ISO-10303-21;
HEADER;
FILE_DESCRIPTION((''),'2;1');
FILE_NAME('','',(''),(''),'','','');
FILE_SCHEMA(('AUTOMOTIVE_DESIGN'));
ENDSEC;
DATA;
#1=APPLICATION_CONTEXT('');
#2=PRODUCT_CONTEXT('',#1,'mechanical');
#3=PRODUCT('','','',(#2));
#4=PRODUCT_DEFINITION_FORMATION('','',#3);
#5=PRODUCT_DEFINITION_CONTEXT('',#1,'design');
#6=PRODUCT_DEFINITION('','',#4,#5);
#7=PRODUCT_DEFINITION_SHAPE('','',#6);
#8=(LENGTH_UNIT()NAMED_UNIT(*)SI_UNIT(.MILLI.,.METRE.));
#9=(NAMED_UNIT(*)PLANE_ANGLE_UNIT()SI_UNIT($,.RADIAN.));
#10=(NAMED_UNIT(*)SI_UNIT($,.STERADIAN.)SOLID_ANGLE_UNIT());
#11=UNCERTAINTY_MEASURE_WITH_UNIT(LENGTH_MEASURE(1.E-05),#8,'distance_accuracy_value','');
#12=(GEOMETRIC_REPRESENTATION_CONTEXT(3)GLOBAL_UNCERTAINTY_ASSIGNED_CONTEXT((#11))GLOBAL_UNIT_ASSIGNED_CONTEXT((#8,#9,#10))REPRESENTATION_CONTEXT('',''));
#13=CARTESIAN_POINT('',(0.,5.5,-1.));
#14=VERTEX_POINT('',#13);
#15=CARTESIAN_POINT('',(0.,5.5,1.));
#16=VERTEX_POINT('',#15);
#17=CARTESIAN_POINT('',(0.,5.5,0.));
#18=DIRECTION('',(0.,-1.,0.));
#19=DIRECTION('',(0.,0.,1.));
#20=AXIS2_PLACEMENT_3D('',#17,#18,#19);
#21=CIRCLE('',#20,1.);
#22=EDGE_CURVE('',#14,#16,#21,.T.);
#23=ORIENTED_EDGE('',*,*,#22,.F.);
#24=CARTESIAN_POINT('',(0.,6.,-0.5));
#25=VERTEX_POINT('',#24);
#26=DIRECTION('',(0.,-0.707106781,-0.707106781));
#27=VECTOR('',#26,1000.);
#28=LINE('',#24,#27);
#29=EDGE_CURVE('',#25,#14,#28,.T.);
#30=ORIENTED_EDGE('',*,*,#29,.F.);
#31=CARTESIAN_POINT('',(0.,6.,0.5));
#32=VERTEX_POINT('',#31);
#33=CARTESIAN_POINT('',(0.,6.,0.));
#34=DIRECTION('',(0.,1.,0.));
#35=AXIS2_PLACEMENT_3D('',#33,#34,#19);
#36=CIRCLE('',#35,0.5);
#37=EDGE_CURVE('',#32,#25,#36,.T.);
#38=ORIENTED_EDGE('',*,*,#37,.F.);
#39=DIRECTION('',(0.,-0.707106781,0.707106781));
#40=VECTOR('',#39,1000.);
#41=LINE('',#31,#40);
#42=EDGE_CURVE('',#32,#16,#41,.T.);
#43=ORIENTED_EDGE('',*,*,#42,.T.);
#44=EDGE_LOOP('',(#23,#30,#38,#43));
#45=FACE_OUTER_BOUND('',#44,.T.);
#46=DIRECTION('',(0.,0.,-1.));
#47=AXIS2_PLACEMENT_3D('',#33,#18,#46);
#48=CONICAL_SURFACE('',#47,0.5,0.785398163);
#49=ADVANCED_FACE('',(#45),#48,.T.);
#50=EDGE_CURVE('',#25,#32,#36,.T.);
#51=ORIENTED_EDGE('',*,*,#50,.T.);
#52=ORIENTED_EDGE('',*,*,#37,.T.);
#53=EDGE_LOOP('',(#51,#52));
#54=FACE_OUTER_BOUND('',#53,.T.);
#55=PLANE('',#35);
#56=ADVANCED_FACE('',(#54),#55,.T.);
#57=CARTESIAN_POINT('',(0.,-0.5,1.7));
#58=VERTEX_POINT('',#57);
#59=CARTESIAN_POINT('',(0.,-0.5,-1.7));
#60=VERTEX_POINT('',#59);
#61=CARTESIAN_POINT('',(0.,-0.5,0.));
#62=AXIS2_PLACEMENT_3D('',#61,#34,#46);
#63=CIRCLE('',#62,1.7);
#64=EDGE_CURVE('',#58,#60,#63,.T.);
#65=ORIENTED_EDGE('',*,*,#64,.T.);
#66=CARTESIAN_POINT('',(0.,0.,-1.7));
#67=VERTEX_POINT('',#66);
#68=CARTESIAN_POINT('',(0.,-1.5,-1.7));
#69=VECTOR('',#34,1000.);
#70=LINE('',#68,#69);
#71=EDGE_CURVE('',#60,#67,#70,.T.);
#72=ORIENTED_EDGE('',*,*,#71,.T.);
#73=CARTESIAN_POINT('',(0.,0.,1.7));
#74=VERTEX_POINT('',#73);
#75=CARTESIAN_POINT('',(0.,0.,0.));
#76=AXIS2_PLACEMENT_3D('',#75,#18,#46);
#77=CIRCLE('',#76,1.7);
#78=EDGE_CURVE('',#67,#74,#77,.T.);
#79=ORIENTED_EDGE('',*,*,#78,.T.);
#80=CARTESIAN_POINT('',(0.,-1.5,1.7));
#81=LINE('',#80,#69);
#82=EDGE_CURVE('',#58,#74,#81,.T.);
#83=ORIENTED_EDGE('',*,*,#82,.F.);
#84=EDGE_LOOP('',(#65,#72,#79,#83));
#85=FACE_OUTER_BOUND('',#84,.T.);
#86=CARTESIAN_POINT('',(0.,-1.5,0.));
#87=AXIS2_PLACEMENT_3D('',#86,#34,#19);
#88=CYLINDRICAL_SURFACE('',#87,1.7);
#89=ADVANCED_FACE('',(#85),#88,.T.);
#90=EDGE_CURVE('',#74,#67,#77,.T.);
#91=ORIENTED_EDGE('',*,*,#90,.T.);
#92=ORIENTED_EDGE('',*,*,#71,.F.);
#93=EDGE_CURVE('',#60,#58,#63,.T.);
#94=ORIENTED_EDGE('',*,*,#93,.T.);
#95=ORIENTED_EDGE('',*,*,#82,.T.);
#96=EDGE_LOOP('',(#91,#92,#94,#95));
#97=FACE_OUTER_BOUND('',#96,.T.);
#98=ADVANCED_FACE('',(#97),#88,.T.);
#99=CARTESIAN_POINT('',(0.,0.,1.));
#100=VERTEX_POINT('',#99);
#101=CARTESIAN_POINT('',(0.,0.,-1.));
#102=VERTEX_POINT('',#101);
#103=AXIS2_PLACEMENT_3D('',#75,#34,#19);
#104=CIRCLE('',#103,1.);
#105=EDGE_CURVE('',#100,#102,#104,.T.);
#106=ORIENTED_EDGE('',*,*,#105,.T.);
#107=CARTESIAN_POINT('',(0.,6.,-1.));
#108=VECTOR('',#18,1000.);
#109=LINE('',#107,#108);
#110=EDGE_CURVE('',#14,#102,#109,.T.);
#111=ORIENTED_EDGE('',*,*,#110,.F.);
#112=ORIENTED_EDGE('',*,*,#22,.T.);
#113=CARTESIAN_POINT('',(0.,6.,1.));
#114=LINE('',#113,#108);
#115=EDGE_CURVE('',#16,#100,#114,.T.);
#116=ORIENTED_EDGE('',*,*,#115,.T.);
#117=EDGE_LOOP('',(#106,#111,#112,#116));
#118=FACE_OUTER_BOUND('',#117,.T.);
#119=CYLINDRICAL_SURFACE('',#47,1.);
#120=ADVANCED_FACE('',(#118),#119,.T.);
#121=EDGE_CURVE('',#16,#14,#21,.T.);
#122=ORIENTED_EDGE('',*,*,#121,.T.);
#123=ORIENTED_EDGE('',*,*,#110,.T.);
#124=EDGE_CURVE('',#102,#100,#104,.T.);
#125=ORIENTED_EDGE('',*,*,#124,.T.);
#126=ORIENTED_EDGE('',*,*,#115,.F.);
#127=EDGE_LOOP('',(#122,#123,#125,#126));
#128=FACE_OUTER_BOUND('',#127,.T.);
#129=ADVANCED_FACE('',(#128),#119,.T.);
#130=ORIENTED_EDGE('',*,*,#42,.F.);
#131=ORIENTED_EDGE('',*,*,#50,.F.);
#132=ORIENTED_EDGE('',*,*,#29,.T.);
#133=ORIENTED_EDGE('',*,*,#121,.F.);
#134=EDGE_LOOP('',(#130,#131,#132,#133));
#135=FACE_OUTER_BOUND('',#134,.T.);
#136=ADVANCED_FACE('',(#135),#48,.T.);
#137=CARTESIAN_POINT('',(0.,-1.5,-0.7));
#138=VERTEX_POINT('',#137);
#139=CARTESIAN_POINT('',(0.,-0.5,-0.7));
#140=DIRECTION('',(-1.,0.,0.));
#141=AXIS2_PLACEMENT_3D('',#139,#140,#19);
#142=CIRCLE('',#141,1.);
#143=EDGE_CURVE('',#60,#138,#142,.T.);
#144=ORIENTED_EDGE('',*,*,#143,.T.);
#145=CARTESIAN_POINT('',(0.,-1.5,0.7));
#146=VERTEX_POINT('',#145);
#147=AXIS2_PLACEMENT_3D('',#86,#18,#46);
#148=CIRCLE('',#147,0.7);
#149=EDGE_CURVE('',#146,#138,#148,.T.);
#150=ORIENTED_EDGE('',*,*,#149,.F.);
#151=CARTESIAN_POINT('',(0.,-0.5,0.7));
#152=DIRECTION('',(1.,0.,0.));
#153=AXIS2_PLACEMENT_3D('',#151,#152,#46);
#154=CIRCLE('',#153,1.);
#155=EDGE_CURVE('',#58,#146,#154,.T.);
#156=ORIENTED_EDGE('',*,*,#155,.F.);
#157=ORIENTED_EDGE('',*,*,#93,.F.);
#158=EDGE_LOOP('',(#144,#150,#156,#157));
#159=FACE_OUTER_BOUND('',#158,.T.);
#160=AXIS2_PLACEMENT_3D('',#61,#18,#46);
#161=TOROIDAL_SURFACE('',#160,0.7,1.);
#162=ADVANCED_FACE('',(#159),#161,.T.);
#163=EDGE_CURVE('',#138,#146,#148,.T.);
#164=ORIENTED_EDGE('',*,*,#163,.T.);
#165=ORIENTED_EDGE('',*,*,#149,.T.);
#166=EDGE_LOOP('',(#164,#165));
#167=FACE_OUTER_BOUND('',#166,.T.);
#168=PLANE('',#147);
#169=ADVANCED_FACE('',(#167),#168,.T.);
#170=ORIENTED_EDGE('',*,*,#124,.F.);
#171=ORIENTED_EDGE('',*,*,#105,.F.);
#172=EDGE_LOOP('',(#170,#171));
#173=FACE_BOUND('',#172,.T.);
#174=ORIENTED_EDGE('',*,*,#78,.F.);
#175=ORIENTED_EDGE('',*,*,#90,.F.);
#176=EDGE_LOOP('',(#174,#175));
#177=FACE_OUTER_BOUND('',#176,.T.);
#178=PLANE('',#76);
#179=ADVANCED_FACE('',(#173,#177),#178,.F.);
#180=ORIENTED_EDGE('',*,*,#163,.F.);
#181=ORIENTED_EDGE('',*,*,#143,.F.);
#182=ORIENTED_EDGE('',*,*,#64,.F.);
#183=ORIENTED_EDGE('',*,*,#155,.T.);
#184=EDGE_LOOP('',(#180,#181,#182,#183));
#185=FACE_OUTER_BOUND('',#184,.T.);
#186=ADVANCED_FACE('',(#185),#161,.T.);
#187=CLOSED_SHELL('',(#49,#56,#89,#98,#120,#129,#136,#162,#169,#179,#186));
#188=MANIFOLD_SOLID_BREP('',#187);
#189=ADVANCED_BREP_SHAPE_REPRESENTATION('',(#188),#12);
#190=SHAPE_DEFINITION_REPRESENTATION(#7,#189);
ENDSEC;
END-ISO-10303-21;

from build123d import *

# Parameters (mm, degrees)
SKETCH1_R           = 1
BOSS_EXTRUDE1_DEPTH = 6
CHAMFER1_SIZE       = 0.5
SKETCH2_R           = 1.7
BOSS_EXTRUDE2_DEPTH = 1.5
FILLET1_R           = 1


with BuildPart() as part:
    # Sketch1 → Boss-Extrude1 (new body)
    with BuildSketch(Plane(origin=(0, 0, 0), x_dir=(1, 0, 0), z_dir=(0, 1, 0))):
        with Locations(Location((0, 0, 0), (0, 0, 270))):
            Circle(SKETCH1_R)
    extrude(amount=BOSS_EXTRUDE1_DEPTH)

    # Chamfer1
    chamfer1_edges = [part.edges().sort_by_distance(p)[0] for p in [
        (0, 6, -1),
    ]]
    chamfer(chamfer1_edges, length=CHAMFER1_SIZE)

    # Sketch2 → Boss-Extrude2 (add)
    with BuildSketch(Plane.XZ):
        with Locations(Location((0, 0, 0), (0, 0, 270))):
            Circle(SKETCH2_R)
    extrude(amount=BOSS_EXTRUDE2_DEPTH)

    # Fillet1
    fillet1_edges = [part.edges().sort_by_distance(p)[0] for p in [
        (0, -1.5, 1.7),
    ]]
    fillet(fillet1_edges, radius=FILLET1_R)


solid = part.part
